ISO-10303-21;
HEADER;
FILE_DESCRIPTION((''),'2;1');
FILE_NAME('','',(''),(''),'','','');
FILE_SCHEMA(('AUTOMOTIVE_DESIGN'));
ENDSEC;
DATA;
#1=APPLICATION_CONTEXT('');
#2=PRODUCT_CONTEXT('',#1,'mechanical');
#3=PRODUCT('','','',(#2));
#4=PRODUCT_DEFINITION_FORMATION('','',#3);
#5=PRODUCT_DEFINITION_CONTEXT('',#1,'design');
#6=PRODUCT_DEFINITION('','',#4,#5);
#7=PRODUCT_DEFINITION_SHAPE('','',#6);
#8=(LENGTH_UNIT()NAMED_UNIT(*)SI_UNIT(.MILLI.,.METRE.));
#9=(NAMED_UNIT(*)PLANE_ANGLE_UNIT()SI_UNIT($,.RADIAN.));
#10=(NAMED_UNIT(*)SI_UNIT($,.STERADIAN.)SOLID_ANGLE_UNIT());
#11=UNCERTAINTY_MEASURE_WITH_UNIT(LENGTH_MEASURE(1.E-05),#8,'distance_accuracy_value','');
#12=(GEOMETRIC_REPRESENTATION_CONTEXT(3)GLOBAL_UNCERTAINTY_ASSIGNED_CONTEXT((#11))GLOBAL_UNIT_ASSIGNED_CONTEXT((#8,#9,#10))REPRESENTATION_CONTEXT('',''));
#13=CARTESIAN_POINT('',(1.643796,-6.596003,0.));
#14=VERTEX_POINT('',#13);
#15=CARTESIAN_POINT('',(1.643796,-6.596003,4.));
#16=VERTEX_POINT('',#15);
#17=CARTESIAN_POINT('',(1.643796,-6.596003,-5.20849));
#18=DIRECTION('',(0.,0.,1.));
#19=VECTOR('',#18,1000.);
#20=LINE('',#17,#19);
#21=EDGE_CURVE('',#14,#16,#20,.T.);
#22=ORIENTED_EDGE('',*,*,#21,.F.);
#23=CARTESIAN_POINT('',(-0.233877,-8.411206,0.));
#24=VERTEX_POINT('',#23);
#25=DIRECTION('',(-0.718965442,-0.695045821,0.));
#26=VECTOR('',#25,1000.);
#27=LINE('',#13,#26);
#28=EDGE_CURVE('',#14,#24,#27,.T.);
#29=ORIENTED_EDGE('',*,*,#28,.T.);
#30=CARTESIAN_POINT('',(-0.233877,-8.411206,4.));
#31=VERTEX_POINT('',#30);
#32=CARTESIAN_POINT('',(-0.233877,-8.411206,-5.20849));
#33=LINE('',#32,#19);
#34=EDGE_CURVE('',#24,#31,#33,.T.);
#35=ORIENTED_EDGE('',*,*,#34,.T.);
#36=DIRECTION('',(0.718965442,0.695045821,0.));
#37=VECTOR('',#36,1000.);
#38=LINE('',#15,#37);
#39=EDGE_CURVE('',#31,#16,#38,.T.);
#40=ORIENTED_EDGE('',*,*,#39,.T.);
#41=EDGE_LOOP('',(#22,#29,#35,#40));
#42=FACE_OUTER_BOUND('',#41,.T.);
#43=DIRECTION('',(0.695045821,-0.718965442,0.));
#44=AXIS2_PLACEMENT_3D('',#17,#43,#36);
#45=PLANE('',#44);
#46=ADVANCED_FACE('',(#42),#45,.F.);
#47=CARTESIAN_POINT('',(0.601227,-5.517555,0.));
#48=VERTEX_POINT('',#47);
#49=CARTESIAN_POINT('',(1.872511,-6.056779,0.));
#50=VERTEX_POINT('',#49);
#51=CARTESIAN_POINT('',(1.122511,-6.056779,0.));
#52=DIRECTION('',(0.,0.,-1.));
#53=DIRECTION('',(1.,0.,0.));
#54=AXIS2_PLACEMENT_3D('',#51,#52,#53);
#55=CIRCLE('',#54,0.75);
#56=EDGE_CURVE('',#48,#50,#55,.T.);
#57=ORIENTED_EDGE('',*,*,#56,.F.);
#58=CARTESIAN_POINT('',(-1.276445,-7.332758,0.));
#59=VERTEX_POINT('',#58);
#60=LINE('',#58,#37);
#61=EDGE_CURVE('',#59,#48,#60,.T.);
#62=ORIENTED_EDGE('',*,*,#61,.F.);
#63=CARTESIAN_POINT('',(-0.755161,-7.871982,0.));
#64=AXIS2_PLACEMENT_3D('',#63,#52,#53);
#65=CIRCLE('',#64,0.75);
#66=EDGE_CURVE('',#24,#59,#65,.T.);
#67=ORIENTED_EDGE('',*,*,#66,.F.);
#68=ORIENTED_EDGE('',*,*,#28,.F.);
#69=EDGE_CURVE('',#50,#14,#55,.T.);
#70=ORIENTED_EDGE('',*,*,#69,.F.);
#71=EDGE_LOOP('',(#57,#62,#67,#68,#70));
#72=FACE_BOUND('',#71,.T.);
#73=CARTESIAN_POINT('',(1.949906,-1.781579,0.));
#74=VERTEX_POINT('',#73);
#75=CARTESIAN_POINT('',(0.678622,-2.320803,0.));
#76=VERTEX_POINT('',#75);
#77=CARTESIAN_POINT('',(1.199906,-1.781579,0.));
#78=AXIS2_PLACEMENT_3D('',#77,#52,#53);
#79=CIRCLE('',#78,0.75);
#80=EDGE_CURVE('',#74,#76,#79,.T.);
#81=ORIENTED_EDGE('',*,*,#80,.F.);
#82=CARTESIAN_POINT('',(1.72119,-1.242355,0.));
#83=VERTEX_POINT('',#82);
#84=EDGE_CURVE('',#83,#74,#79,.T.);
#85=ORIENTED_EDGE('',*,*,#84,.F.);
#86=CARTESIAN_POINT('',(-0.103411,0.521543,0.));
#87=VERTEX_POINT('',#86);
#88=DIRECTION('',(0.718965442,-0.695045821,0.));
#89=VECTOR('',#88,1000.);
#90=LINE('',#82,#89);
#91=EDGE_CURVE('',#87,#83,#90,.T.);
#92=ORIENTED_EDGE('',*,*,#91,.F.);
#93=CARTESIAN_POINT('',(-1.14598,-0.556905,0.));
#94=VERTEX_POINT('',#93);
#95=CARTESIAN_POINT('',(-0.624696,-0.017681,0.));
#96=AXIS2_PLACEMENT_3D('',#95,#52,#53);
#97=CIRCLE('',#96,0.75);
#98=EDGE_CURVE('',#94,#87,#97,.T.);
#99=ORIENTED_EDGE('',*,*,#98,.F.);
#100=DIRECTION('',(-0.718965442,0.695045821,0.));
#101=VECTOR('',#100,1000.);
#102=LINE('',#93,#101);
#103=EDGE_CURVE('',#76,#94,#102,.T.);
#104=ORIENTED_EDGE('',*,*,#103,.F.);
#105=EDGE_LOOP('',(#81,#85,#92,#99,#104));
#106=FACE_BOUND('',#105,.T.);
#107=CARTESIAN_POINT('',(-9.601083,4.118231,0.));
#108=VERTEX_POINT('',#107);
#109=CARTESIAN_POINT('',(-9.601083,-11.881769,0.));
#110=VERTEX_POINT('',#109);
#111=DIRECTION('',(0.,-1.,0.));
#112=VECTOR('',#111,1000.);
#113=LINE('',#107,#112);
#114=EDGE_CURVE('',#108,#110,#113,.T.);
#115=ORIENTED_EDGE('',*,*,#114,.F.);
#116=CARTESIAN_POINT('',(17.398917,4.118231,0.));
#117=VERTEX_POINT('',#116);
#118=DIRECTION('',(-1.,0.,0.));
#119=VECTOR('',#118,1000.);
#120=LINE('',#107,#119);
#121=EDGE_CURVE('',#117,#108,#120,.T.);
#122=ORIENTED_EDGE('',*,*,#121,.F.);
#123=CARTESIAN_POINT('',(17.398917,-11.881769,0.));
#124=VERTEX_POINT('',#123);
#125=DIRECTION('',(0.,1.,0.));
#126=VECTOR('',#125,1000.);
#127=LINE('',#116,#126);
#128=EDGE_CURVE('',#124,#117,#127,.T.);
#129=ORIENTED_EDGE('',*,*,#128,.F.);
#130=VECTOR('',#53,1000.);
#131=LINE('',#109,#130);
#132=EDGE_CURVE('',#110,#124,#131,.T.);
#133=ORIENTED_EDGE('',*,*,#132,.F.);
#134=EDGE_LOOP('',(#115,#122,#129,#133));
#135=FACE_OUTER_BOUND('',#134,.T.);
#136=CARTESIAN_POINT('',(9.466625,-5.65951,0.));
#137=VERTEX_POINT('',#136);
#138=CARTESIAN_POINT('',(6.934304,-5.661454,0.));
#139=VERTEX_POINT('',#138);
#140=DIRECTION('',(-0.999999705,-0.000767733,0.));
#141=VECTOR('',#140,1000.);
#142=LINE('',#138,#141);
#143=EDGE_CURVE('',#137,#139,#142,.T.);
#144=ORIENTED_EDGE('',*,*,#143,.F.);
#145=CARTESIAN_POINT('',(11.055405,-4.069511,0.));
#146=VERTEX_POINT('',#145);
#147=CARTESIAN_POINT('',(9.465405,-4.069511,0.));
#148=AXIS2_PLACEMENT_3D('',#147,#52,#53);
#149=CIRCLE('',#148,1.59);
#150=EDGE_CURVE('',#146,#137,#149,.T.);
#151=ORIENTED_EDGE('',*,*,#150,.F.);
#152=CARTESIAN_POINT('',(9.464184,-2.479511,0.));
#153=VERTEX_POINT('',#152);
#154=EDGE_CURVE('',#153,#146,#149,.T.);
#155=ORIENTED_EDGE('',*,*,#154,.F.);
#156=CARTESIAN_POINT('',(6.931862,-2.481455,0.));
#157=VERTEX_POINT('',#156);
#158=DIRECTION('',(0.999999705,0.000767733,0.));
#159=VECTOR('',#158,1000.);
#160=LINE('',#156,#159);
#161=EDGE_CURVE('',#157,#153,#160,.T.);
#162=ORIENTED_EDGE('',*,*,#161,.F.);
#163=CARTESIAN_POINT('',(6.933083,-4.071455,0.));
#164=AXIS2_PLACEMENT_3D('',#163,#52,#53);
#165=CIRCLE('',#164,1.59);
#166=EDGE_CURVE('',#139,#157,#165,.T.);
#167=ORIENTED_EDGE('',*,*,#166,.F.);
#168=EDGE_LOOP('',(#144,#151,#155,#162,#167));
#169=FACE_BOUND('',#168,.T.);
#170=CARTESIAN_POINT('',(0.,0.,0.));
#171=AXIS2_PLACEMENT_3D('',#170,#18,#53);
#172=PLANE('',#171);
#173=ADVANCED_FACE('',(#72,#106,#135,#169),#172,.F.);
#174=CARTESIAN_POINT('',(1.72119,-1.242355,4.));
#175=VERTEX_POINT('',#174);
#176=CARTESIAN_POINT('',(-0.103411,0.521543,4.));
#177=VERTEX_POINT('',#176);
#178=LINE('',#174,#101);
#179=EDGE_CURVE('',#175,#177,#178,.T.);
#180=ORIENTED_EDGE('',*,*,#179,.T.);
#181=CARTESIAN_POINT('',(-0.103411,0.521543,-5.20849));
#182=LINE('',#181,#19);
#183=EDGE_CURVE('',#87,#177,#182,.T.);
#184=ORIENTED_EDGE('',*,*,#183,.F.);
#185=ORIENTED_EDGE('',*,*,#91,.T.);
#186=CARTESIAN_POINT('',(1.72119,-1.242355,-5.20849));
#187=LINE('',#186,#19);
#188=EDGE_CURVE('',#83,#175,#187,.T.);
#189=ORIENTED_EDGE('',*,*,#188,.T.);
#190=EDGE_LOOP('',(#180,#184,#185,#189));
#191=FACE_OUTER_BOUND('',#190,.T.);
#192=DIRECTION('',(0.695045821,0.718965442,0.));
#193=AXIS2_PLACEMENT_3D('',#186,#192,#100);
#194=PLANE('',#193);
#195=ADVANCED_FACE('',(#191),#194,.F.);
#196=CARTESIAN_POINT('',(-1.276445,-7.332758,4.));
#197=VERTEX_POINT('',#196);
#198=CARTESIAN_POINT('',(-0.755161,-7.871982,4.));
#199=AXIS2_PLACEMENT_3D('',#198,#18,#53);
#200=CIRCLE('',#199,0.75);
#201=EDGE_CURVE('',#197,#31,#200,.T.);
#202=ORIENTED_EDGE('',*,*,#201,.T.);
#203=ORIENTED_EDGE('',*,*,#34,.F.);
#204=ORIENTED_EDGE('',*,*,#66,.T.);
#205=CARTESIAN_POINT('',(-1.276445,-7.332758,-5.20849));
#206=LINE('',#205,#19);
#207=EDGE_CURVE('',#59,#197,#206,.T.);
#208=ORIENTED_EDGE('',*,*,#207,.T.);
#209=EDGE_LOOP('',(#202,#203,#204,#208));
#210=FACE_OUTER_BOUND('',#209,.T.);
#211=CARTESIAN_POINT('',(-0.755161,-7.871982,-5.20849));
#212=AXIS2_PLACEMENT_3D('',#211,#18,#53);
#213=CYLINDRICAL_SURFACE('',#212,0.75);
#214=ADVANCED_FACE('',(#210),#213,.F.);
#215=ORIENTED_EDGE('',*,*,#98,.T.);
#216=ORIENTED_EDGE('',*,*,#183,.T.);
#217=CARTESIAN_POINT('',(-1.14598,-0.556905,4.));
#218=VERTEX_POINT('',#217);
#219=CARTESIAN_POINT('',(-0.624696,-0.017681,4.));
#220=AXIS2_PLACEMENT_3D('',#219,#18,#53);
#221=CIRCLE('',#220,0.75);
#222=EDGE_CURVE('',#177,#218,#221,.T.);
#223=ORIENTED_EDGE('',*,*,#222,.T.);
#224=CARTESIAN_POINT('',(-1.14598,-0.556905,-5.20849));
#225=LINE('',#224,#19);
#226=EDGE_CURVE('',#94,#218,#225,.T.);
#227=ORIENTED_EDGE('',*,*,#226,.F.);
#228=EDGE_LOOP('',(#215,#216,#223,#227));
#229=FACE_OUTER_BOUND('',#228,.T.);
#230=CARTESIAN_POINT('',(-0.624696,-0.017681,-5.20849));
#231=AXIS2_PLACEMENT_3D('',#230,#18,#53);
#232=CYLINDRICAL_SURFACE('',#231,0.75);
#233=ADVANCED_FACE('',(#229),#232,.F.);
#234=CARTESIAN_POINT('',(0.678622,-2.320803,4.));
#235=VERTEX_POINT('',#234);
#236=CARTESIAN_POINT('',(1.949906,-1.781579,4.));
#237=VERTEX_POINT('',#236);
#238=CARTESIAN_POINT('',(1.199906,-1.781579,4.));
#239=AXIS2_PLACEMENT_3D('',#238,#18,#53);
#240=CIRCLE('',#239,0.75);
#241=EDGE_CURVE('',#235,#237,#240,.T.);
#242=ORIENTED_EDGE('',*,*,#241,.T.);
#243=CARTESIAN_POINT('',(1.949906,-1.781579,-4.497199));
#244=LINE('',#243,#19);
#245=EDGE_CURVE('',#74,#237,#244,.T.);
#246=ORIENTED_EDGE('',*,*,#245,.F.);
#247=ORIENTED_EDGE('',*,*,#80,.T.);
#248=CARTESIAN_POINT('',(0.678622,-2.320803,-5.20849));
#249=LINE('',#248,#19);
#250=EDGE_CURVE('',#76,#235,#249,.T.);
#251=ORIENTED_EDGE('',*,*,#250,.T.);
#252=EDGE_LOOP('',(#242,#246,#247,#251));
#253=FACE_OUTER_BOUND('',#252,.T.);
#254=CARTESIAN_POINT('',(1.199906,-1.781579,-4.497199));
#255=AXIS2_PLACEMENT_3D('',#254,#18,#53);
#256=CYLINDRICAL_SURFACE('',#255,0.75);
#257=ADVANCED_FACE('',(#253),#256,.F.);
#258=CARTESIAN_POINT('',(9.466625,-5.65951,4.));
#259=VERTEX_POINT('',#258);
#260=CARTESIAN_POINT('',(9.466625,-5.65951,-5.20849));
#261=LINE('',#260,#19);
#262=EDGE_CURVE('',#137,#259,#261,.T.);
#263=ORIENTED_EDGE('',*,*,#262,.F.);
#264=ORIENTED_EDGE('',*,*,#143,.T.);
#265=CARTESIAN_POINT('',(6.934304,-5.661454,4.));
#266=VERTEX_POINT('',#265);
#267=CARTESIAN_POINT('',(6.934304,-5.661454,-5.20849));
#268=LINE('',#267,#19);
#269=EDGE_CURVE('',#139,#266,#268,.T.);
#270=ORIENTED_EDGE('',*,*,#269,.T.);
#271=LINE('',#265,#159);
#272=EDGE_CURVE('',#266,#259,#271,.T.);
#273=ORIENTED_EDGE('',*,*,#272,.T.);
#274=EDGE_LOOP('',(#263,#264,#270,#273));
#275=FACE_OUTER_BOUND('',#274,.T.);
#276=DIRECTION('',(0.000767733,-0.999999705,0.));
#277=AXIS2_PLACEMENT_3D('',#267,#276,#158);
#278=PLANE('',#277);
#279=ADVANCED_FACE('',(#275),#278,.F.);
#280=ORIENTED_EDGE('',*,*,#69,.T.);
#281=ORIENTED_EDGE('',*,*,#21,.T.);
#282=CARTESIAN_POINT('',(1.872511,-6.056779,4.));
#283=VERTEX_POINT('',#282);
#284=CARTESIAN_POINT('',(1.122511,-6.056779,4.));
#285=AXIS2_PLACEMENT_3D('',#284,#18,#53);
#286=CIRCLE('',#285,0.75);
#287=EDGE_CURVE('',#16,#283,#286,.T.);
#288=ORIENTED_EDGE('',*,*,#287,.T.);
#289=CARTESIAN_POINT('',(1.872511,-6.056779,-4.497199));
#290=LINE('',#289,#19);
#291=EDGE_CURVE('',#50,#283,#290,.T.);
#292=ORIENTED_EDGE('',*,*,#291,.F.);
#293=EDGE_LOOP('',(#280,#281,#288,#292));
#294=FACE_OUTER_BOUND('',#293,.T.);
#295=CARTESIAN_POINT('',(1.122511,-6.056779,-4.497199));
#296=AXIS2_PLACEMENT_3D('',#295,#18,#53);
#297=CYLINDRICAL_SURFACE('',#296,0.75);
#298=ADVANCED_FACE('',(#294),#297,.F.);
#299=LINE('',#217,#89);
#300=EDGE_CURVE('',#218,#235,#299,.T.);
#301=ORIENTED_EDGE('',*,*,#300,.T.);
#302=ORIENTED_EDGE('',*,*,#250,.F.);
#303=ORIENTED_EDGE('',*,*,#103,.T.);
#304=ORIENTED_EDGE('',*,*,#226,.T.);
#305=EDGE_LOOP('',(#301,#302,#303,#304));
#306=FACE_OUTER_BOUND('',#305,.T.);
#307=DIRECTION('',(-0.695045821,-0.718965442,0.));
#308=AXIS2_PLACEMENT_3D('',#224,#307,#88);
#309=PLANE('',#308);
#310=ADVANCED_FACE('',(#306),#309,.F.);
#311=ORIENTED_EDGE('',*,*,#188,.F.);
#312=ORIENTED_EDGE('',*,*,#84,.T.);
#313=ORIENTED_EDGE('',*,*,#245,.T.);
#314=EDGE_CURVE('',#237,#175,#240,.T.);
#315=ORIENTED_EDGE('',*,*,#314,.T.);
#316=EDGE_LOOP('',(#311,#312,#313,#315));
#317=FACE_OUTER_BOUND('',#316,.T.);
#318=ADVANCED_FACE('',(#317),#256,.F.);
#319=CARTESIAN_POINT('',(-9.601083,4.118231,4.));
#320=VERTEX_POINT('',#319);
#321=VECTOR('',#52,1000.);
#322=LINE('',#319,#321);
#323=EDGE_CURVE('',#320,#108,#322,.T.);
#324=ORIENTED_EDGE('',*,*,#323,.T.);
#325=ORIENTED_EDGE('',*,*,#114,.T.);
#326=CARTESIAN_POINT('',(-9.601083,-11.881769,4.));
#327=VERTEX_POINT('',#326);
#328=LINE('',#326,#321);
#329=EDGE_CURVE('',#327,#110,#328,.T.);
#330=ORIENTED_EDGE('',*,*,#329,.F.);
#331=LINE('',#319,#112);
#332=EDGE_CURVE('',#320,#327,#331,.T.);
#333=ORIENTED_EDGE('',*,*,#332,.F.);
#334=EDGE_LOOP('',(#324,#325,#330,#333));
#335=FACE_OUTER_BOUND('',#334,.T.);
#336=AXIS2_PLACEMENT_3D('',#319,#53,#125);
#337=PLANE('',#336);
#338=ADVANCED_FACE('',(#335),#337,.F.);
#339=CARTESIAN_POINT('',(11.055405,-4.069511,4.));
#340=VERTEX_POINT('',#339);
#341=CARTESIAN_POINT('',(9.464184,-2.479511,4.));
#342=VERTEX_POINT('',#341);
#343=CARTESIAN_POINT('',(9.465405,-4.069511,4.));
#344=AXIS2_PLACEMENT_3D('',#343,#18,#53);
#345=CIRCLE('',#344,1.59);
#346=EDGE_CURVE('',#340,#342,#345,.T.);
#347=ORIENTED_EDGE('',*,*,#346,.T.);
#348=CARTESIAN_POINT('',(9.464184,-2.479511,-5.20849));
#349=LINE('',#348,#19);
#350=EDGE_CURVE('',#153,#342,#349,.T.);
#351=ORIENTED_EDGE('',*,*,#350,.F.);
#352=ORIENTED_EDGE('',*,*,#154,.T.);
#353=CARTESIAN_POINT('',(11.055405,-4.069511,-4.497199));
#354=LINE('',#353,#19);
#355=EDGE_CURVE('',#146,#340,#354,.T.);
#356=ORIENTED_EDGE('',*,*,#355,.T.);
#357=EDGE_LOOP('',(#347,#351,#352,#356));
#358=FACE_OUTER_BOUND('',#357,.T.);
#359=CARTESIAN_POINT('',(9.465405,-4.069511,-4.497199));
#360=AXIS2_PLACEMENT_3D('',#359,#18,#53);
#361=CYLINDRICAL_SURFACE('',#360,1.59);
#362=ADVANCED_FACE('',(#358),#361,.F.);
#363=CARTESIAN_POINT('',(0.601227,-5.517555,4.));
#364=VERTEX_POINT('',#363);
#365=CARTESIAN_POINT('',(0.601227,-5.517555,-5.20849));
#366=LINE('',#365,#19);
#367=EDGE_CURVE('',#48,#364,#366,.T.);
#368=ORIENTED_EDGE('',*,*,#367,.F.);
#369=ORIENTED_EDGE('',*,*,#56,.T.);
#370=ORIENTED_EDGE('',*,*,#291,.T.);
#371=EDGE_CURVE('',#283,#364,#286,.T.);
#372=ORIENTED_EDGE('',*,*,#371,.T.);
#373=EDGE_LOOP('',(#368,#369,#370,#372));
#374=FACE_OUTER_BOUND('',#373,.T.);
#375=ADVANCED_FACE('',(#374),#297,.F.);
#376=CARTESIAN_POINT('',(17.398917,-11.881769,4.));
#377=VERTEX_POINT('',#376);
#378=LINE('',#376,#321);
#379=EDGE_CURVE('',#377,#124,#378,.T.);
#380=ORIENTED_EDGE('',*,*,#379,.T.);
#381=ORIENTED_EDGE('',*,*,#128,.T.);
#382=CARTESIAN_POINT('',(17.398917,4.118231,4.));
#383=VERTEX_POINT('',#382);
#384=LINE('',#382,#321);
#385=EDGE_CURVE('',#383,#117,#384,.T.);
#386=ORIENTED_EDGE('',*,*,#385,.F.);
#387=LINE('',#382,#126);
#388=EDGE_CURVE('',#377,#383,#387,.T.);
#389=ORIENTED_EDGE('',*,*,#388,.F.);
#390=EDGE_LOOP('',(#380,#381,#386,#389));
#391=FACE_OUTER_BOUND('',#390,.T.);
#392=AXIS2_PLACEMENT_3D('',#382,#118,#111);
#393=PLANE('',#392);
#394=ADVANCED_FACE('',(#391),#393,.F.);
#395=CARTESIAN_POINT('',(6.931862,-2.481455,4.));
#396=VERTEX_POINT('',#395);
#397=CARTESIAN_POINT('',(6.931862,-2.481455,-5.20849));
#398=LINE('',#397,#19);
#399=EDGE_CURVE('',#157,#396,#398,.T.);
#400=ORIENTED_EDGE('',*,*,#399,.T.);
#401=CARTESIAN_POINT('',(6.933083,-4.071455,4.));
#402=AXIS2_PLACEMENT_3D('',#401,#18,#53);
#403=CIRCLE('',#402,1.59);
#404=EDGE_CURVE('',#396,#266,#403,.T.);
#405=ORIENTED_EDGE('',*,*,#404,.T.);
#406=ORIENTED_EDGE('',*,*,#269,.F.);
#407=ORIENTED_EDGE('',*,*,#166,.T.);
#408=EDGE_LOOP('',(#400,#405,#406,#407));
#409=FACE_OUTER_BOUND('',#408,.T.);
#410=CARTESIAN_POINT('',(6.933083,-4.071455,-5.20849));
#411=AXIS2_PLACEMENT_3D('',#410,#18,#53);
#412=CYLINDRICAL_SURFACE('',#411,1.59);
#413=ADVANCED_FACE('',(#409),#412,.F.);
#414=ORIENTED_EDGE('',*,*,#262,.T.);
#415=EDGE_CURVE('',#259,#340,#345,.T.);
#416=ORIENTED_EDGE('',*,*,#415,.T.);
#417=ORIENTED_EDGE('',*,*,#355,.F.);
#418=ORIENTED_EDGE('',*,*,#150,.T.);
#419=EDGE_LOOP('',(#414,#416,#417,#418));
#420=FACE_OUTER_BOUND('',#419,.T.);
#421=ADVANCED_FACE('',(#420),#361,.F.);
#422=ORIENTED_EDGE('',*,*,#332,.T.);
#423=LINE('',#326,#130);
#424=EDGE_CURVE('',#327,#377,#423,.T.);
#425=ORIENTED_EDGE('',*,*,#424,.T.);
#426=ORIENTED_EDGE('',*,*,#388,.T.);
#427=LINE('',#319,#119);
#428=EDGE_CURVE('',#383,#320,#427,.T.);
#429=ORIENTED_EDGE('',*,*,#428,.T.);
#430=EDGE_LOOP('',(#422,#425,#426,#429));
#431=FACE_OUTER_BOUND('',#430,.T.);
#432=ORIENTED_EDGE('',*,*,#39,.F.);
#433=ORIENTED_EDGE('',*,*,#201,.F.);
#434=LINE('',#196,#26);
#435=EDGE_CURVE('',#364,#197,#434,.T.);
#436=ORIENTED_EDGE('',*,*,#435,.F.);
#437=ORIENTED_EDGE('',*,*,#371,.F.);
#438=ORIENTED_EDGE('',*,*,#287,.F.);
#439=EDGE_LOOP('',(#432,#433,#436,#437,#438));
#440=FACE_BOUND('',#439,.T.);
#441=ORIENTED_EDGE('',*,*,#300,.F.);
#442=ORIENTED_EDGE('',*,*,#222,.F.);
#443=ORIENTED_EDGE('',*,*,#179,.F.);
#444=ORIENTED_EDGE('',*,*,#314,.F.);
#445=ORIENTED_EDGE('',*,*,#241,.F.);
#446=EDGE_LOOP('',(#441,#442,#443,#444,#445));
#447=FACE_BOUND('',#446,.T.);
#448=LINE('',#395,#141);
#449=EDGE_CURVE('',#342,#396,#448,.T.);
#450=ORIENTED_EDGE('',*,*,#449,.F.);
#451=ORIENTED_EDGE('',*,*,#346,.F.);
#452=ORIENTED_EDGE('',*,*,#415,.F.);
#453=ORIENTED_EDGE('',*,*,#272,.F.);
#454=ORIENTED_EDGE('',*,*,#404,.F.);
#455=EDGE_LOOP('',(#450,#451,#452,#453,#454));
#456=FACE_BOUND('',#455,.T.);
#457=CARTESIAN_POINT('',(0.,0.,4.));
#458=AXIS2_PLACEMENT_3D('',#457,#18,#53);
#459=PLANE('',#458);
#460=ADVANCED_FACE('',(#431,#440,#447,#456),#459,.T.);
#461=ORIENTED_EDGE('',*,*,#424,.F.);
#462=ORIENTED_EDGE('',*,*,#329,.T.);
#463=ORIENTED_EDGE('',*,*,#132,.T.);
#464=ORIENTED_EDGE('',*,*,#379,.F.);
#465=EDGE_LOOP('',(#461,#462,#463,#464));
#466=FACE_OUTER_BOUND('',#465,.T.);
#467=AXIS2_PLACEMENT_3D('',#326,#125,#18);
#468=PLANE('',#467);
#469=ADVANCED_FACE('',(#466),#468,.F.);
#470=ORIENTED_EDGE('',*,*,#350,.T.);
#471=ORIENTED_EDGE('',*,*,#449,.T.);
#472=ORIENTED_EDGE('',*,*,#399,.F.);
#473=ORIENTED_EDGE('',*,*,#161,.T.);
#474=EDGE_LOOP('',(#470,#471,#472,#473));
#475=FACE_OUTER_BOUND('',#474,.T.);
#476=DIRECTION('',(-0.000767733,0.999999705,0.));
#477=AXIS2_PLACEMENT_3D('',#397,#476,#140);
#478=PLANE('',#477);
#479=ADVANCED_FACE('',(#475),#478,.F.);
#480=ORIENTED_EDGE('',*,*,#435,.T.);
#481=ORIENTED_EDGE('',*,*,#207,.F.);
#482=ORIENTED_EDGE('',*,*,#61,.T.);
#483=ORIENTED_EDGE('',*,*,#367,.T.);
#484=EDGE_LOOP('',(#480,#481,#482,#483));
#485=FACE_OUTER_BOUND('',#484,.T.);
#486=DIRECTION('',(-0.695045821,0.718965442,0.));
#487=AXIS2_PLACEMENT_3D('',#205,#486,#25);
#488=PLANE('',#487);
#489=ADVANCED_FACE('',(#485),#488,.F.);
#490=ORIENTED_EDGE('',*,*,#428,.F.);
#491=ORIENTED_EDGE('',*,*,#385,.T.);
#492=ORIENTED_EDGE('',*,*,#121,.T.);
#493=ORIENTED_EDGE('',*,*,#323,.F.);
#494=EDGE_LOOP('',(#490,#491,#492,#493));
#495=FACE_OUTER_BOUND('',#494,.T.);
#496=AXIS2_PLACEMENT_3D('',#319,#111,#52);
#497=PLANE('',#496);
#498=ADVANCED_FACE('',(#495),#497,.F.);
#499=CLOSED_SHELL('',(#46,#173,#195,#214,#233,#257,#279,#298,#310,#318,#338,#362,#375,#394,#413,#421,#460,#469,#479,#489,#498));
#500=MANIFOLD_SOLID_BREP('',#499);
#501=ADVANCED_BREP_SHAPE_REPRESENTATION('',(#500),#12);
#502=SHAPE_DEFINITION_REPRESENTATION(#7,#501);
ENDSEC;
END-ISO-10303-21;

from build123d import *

# Parameters (mm, degrees)
SKETCH_1_W          = 27
SKETCH_1_H          = 16
EXTRUDE_1_DEPTH     = 4
SKETCH_2_R          = 0.75
SKETCH_2_R_2        = 1.59
CUT_EXTRUDE_2_DEPTH = 4
CUT_EXTRUDE_3_DEPTH = 4


with BuildPart() as part:
    # 草图1 → 凸台-拉伸1 (new body)
    with BuildSketch(Plane.XY):
        with Locations((3.898916968, -3.881768953)):
            Rectangle(SKETCH_1_W, SKETCH_1_H)
    extrude(amount=EXTRUDE_1_DEPTH)

    # 草图2 → 切除-拉伸2 (cut)
    with BuildSketch(Plane.XY.offset(4)):
        with Locations((1.199905932, -1.781578746)):
            Circle(SKETCH_2_R)
        with Locations((1.122511443, -6.056778774)):
            Circle(SKETCH_2_R)
        with Locations((9.465404763, -4.069510677)):
            Circle(SKETCH_2_R_2)
    extrude(amount=-CUT_EXTRUDE_2_DEPTH, mode=Mode.SUBTRACT)

    # 草图3 → 切除-拉伸3 (cut)
    with BuildSketch(Plane.XY.offset(4)):
        with BuildLine():
            Line((6.931862452, -2.481455291), (9.464184068, -2.479511145))
            ThreePointArc((9.464184068, -2.479511145), (7.875405231, -4.070731371), (9.466625457, -5.659510208))
            Line((9.466625457, -5.659510208), (6.934303841, -5.661454354))
            ThreePointArc((6.934303841, -5.661454354), (5.343083615, -4.072675517), (6.931862452, -2.481455291))
        make_face()
        with BuildLine():
            Line((-1.276445305, -7.332757851), (0.601227077, -5.517554692))
            ThreePointArc((0.601227077, -5.517554692), (0.583287361, -6.578063139), (1.643795809, -6.596002856))
            Line((1.643795809, -6.596002856), (-0.233876574, -8.411206015))
            ThreePointArc((-0.233876574, -8.411206015), (-1.294385021, -8.393266299), (-1.276445305, -7.332757851))
        make_face()
        with BuildLine():
            Line((-1.145979965, -0.556904877), (0.678621567, -2.320802827))
            ThreePointArc((0.678621567, -2.320802827), (0.660681851, -1.26029438), (1.721190298, -1.242354664))
            Line((1.721190298, -1.242354664), (-0.103411234, 0.521543286))
            ThreePointArc((-0.103411234, 0.521543286), (-1.163919681, 0.50360357), (-1.145979965, -0.556904877))
        make_face()
    extrude(amount=-CUT_EXTRUDE_3_DEPTH, mode=Mode.SUBTRACT)


solid = part.part
